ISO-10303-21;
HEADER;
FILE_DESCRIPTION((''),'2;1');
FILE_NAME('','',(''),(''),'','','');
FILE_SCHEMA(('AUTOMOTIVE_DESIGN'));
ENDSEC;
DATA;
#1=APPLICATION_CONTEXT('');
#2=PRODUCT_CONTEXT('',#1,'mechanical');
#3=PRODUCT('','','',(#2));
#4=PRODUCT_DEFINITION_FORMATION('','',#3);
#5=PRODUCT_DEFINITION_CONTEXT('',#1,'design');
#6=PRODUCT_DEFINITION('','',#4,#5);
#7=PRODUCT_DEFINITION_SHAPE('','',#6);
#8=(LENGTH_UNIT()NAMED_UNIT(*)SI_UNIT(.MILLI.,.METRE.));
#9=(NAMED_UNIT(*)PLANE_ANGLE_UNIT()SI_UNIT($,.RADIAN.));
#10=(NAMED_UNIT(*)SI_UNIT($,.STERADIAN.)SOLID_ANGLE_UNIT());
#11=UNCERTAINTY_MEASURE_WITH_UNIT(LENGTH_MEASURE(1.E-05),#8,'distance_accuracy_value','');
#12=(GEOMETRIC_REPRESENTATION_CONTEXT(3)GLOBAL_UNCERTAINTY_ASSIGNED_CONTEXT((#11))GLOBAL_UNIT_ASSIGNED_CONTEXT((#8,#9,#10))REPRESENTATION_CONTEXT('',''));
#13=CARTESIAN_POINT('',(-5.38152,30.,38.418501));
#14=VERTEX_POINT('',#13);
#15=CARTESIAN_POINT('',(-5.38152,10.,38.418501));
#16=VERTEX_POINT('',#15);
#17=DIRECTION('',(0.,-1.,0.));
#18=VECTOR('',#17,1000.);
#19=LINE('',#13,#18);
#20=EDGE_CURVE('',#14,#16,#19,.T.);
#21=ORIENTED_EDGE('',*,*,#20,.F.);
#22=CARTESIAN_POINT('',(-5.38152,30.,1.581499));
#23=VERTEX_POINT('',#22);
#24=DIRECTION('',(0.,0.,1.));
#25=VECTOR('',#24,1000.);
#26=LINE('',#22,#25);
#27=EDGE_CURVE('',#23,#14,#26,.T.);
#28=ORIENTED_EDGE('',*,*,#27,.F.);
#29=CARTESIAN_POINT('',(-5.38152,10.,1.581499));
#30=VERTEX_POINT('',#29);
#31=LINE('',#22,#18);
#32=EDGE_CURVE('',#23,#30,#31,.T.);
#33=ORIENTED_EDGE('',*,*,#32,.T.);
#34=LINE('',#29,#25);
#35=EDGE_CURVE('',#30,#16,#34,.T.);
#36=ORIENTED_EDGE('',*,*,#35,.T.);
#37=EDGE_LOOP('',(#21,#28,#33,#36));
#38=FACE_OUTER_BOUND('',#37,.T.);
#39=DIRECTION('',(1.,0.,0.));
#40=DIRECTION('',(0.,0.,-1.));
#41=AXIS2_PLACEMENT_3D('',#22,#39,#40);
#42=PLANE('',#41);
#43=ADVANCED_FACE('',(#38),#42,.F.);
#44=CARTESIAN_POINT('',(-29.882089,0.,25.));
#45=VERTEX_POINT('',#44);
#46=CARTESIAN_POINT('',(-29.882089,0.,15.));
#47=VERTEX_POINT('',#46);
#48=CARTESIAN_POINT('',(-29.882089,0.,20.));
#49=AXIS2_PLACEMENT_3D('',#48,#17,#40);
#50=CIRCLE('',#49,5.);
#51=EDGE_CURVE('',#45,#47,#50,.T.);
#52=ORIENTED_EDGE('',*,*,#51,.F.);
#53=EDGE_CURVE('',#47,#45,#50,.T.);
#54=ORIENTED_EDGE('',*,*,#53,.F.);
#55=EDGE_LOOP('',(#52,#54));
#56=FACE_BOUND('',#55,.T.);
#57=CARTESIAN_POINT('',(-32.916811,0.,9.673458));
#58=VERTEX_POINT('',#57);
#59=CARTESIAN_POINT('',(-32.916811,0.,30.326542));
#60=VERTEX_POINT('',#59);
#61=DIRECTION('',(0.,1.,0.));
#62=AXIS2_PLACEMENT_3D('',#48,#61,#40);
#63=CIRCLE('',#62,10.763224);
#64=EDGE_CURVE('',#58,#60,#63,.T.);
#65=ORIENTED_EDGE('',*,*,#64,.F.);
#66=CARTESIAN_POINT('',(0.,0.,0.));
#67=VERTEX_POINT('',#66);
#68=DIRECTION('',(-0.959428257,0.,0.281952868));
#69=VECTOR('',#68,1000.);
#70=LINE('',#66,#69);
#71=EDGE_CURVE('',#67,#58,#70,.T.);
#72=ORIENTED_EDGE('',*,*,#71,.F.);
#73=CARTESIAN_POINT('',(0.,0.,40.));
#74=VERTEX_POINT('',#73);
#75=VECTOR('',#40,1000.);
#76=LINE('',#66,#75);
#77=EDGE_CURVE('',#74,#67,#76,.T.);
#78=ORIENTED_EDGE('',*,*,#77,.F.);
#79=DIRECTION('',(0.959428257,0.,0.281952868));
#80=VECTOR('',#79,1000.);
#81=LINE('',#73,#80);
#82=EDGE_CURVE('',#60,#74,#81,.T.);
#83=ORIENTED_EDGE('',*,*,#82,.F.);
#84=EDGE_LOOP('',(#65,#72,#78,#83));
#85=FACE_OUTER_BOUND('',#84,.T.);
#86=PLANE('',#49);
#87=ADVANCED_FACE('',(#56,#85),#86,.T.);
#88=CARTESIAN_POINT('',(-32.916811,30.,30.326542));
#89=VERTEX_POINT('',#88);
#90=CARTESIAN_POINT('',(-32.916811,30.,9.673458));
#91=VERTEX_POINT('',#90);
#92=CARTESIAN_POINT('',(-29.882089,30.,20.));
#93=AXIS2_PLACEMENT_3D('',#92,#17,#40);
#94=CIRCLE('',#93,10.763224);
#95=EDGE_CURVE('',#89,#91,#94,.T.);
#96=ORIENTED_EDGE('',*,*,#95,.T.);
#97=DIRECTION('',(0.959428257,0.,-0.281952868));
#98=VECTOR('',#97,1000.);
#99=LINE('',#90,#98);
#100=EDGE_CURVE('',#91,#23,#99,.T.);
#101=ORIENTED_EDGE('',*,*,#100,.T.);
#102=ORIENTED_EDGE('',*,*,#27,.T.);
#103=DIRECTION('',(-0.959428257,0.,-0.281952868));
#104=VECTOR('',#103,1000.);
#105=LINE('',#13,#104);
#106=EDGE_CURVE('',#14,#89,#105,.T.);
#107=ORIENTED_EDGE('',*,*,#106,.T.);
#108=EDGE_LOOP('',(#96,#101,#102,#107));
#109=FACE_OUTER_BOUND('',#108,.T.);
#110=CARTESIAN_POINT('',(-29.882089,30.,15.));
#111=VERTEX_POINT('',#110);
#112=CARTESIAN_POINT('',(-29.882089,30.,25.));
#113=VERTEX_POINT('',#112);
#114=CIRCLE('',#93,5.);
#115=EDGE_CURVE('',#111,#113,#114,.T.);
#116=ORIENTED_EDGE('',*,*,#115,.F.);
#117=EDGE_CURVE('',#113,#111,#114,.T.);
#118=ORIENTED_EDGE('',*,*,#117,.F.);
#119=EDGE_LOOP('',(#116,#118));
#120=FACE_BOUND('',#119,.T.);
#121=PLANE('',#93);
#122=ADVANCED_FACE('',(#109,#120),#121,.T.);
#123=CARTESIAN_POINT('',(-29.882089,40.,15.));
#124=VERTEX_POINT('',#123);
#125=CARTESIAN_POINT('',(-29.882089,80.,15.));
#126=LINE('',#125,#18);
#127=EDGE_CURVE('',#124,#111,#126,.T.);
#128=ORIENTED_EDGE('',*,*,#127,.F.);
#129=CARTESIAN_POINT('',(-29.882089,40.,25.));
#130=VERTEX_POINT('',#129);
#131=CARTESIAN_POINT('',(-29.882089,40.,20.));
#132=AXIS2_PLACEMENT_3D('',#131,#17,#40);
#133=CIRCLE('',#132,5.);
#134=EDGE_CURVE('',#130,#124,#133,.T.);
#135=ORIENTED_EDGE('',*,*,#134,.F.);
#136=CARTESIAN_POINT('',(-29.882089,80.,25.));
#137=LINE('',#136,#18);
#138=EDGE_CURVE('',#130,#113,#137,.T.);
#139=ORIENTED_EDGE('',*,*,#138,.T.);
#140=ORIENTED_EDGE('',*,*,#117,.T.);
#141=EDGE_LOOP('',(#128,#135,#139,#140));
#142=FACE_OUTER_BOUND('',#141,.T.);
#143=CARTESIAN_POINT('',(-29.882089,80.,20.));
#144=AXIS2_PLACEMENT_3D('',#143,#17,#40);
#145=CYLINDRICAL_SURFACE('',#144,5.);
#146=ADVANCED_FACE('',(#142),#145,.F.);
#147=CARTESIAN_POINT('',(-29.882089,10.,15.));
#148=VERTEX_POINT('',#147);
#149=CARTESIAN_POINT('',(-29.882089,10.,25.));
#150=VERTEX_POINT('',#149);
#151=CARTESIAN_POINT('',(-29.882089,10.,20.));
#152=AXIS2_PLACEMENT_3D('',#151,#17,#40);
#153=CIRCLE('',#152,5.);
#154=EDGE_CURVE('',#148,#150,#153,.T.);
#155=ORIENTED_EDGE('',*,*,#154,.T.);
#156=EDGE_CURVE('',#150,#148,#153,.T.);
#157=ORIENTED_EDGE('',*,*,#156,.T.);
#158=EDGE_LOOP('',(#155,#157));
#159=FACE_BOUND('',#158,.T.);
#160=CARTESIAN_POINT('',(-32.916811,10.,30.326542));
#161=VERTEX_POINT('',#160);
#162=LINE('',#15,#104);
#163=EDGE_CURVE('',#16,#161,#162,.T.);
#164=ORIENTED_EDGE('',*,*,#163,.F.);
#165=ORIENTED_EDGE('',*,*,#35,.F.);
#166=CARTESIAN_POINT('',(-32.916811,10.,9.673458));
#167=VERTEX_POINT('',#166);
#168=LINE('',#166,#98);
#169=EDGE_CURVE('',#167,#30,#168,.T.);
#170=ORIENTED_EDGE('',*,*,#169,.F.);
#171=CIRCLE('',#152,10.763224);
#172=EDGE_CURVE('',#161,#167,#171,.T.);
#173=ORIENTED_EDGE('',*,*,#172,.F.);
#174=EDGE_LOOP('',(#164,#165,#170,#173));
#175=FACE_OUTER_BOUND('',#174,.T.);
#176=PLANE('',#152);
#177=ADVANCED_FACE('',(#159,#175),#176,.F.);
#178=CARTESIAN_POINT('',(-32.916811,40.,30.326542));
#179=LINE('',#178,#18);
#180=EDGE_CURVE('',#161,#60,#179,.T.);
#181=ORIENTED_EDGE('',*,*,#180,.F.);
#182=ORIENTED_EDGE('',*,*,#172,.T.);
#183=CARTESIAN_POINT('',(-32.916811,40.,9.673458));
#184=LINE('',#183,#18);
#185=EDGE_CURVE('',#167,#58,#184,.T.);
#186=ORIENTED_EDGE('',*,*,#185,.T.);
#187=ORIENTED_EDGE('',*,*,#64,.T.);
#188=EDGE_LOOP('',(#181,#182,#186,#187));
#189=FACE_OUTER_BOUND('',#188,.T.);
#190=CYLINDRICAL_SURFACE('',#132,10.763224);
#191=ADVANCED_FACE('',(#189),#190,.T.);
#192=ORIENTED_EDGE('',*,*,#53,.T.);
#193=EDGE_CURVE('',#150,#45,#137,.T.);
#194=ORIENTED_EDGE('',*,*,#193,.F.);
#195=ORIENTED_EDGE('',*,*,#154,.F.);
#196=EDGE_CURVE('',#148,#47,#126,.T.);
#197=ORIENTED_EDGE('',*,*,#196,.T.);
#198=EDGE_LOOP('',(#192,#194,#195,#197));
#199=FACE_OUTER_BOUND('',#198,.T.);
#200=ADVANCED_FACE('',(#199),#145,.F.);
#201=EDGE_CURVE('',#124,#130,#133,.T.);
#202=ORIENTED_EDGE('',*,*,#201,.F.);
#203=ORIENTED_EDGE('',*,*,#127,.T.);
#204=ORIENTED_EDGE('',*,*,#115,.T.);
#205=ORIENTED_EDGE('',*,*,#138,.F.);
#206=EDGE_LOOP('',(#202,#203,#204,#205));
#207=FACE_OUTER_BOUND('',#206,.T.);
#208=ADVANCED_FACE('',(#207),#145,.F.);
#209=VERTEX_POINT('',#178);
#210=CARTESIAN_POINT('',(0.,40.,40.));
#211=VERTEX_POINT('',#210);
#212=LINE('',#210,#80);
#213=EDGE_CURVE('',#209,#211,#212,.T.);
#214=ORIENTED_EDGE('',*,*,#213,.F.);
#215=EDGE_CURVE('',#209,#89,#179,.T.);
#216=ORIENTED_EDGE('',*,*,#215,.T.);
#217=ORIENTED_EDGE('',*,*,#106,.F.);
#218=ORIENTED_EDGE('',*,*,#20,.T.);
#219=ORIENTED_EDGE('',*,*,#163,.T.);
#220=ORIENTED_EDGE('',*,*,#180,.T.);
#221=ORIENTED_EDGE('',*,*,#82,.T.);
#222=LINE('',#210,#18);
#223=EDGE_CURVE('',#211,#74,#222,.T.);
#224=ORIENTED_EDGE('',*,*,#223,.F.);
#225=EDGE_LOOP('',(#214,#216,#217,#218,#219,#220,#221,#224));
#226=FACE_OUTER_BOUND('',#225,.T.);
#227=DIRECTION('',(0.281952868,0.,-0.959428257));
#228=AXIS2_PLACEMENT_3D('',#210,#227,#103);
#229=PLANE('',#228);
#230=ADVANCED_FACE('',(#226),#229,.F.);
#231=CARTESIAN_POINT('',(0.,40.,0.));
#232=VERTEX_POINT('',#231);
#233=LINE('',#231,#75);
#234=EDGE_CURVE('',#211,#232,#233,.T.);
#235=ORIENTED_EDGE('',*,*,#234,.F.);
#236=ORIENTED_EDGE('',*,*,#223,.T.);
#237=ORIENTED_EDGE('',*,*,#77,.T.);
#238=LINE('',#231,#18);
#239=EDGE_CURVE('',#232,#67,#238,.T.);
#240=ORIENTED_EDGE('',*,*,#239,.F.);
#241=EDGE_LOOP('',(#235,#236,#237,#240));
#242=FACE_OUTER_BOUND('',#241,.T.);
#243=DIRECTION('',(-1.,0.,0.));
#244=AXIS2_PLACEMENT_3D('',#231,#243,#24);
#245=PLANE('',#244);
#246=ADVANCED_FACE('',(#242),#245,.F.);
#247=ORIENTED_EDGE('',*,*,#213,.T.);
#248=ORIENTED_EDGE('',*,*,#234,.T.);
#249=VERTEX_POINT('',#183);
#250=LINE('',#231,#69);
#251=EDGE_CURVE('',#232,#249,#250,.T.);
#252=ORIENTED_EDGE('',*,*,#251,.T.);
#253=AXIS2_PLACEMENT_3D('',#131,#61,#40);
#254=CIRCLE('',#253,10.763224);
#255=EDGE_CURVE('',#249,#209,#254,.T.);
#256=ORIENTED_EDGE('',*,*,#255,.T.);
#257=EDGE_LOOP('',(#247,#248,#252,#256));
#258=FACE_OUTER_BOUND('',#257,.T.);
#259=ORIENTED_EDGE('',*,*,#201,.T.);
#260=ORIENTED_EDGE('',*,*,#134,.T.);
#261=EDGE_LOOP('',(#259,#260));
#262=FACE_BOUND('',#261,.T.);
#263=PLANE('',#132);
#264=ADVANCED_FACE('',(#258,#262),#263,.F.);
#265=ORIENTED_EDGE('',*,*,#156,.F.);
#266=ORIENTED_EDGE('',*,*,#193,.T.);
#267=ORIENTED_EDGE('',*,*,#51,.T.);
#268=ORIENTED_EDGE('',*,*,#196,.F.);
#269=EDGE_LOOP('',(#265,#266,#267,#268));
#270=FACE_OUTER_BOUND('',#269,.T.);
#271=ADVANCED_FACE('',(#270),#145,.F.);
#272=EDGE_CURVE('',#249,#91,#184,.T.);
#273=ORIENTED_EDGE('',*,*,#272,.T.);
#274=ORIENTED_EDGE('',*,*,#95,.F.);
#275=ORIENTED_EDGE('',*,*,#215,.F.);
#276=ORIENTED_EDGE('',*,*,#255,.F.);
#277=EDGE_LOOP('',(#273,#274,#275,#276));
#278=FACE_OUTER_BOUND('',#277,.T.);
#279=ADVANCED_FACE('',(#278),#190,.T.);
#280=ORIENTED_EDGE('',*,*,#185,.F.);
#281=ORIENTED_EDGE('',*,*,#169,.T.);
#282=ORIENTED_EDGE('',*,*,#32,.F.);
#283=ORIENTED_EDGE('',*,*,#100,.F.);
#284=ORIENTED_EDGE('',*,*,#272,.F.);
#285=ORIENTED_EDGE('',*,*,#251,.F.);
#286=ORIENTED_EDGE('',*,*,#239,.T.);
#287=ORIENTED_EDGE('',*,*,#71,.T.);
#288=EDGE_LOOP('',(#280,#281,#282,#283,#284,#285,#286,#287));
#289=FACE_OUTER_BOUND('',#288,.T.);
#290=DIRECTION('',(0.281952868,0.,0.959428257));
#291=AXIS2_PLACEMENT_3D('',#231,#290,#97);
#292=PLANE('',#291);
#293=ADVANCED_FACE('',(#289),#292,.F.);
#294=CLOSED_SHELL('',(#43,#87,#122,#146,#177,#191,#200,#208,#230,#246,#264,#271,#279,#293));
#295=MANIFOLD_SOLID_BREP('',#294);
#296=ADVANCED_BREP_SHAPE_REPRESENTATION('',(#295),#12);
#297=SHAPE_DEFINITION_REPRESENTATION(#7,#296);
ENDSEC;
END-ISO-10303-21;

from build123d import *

# Parameters (mm, degrees)
BOSS_EXTRUDE1_DEPTH = 40
CUT_EXTRUDE1_DEPTH  = 20
SKETCH3_R           = 5
CUT_EXTRUDE2_DEPTH  = 70


with BuildPart() as part:
    # Sketch1 → Boss-Extrude1 (new body)
    with BuildSketch(Plane(origin=(0, 0, 0), x_dir=(1, 0, 0), z_dir=(0, 1, 0))):
        with BuildLine():
            Line((0, 0), (0, -40))
            Line((0, -40), (-32.916811342, -30.326541582))
            ThreePointArc((-32.916811342, -30.326541582), (-40.645313725, -20), (-32.916811342, -9.673458418))
            Line((-32.916811342, -9.673458418), (0, 0))
        make_face()
    extrude(amount=BOSS_EXTRUDE1_DEPTH)

    # Sketch2 → Cut-Extrude1 (cut)
    with BuildSketch(Plane(origin=(0, 10, 0), x_dir=(-1, 0, 0), z_dir=(0, -1, 0))):
        with BuildLine():
            Line((5.381519546, -1.581499041), (5.381519546, -38.418500959))
            Line((5.381519546, -38.418500959), (32.916811342, -30.326541582))
            ThreePointArc((32.916811342, -30.326541582), (40.645313725, -20), (32.916811342, -9.673458418))
            Line((32.916811342, -9.673458418), (5.381519546, -1.581499041))
        make_face()
    extrude(amount=-CUT_EXTRUDE1_DEPTH, mode=Mode.SUBTRACT)

    # Sketch3 → Cut-Extrude2 (cut, symmetric)
    with BuildSketch(Plane(origin=(0, 10, 0), x_dir=(-1, 0, 0), z_dir=(0, -1, 0))):
        with Locations(Location((29.882089371, -20, 0), (0, 0, 90))):
            Circle(SKETCH3_R)
    extrude(amount=CUT_EXTRUDE2_DEPTH, both=True, mode=Mode.SUBTRACT)


solid = part.part
